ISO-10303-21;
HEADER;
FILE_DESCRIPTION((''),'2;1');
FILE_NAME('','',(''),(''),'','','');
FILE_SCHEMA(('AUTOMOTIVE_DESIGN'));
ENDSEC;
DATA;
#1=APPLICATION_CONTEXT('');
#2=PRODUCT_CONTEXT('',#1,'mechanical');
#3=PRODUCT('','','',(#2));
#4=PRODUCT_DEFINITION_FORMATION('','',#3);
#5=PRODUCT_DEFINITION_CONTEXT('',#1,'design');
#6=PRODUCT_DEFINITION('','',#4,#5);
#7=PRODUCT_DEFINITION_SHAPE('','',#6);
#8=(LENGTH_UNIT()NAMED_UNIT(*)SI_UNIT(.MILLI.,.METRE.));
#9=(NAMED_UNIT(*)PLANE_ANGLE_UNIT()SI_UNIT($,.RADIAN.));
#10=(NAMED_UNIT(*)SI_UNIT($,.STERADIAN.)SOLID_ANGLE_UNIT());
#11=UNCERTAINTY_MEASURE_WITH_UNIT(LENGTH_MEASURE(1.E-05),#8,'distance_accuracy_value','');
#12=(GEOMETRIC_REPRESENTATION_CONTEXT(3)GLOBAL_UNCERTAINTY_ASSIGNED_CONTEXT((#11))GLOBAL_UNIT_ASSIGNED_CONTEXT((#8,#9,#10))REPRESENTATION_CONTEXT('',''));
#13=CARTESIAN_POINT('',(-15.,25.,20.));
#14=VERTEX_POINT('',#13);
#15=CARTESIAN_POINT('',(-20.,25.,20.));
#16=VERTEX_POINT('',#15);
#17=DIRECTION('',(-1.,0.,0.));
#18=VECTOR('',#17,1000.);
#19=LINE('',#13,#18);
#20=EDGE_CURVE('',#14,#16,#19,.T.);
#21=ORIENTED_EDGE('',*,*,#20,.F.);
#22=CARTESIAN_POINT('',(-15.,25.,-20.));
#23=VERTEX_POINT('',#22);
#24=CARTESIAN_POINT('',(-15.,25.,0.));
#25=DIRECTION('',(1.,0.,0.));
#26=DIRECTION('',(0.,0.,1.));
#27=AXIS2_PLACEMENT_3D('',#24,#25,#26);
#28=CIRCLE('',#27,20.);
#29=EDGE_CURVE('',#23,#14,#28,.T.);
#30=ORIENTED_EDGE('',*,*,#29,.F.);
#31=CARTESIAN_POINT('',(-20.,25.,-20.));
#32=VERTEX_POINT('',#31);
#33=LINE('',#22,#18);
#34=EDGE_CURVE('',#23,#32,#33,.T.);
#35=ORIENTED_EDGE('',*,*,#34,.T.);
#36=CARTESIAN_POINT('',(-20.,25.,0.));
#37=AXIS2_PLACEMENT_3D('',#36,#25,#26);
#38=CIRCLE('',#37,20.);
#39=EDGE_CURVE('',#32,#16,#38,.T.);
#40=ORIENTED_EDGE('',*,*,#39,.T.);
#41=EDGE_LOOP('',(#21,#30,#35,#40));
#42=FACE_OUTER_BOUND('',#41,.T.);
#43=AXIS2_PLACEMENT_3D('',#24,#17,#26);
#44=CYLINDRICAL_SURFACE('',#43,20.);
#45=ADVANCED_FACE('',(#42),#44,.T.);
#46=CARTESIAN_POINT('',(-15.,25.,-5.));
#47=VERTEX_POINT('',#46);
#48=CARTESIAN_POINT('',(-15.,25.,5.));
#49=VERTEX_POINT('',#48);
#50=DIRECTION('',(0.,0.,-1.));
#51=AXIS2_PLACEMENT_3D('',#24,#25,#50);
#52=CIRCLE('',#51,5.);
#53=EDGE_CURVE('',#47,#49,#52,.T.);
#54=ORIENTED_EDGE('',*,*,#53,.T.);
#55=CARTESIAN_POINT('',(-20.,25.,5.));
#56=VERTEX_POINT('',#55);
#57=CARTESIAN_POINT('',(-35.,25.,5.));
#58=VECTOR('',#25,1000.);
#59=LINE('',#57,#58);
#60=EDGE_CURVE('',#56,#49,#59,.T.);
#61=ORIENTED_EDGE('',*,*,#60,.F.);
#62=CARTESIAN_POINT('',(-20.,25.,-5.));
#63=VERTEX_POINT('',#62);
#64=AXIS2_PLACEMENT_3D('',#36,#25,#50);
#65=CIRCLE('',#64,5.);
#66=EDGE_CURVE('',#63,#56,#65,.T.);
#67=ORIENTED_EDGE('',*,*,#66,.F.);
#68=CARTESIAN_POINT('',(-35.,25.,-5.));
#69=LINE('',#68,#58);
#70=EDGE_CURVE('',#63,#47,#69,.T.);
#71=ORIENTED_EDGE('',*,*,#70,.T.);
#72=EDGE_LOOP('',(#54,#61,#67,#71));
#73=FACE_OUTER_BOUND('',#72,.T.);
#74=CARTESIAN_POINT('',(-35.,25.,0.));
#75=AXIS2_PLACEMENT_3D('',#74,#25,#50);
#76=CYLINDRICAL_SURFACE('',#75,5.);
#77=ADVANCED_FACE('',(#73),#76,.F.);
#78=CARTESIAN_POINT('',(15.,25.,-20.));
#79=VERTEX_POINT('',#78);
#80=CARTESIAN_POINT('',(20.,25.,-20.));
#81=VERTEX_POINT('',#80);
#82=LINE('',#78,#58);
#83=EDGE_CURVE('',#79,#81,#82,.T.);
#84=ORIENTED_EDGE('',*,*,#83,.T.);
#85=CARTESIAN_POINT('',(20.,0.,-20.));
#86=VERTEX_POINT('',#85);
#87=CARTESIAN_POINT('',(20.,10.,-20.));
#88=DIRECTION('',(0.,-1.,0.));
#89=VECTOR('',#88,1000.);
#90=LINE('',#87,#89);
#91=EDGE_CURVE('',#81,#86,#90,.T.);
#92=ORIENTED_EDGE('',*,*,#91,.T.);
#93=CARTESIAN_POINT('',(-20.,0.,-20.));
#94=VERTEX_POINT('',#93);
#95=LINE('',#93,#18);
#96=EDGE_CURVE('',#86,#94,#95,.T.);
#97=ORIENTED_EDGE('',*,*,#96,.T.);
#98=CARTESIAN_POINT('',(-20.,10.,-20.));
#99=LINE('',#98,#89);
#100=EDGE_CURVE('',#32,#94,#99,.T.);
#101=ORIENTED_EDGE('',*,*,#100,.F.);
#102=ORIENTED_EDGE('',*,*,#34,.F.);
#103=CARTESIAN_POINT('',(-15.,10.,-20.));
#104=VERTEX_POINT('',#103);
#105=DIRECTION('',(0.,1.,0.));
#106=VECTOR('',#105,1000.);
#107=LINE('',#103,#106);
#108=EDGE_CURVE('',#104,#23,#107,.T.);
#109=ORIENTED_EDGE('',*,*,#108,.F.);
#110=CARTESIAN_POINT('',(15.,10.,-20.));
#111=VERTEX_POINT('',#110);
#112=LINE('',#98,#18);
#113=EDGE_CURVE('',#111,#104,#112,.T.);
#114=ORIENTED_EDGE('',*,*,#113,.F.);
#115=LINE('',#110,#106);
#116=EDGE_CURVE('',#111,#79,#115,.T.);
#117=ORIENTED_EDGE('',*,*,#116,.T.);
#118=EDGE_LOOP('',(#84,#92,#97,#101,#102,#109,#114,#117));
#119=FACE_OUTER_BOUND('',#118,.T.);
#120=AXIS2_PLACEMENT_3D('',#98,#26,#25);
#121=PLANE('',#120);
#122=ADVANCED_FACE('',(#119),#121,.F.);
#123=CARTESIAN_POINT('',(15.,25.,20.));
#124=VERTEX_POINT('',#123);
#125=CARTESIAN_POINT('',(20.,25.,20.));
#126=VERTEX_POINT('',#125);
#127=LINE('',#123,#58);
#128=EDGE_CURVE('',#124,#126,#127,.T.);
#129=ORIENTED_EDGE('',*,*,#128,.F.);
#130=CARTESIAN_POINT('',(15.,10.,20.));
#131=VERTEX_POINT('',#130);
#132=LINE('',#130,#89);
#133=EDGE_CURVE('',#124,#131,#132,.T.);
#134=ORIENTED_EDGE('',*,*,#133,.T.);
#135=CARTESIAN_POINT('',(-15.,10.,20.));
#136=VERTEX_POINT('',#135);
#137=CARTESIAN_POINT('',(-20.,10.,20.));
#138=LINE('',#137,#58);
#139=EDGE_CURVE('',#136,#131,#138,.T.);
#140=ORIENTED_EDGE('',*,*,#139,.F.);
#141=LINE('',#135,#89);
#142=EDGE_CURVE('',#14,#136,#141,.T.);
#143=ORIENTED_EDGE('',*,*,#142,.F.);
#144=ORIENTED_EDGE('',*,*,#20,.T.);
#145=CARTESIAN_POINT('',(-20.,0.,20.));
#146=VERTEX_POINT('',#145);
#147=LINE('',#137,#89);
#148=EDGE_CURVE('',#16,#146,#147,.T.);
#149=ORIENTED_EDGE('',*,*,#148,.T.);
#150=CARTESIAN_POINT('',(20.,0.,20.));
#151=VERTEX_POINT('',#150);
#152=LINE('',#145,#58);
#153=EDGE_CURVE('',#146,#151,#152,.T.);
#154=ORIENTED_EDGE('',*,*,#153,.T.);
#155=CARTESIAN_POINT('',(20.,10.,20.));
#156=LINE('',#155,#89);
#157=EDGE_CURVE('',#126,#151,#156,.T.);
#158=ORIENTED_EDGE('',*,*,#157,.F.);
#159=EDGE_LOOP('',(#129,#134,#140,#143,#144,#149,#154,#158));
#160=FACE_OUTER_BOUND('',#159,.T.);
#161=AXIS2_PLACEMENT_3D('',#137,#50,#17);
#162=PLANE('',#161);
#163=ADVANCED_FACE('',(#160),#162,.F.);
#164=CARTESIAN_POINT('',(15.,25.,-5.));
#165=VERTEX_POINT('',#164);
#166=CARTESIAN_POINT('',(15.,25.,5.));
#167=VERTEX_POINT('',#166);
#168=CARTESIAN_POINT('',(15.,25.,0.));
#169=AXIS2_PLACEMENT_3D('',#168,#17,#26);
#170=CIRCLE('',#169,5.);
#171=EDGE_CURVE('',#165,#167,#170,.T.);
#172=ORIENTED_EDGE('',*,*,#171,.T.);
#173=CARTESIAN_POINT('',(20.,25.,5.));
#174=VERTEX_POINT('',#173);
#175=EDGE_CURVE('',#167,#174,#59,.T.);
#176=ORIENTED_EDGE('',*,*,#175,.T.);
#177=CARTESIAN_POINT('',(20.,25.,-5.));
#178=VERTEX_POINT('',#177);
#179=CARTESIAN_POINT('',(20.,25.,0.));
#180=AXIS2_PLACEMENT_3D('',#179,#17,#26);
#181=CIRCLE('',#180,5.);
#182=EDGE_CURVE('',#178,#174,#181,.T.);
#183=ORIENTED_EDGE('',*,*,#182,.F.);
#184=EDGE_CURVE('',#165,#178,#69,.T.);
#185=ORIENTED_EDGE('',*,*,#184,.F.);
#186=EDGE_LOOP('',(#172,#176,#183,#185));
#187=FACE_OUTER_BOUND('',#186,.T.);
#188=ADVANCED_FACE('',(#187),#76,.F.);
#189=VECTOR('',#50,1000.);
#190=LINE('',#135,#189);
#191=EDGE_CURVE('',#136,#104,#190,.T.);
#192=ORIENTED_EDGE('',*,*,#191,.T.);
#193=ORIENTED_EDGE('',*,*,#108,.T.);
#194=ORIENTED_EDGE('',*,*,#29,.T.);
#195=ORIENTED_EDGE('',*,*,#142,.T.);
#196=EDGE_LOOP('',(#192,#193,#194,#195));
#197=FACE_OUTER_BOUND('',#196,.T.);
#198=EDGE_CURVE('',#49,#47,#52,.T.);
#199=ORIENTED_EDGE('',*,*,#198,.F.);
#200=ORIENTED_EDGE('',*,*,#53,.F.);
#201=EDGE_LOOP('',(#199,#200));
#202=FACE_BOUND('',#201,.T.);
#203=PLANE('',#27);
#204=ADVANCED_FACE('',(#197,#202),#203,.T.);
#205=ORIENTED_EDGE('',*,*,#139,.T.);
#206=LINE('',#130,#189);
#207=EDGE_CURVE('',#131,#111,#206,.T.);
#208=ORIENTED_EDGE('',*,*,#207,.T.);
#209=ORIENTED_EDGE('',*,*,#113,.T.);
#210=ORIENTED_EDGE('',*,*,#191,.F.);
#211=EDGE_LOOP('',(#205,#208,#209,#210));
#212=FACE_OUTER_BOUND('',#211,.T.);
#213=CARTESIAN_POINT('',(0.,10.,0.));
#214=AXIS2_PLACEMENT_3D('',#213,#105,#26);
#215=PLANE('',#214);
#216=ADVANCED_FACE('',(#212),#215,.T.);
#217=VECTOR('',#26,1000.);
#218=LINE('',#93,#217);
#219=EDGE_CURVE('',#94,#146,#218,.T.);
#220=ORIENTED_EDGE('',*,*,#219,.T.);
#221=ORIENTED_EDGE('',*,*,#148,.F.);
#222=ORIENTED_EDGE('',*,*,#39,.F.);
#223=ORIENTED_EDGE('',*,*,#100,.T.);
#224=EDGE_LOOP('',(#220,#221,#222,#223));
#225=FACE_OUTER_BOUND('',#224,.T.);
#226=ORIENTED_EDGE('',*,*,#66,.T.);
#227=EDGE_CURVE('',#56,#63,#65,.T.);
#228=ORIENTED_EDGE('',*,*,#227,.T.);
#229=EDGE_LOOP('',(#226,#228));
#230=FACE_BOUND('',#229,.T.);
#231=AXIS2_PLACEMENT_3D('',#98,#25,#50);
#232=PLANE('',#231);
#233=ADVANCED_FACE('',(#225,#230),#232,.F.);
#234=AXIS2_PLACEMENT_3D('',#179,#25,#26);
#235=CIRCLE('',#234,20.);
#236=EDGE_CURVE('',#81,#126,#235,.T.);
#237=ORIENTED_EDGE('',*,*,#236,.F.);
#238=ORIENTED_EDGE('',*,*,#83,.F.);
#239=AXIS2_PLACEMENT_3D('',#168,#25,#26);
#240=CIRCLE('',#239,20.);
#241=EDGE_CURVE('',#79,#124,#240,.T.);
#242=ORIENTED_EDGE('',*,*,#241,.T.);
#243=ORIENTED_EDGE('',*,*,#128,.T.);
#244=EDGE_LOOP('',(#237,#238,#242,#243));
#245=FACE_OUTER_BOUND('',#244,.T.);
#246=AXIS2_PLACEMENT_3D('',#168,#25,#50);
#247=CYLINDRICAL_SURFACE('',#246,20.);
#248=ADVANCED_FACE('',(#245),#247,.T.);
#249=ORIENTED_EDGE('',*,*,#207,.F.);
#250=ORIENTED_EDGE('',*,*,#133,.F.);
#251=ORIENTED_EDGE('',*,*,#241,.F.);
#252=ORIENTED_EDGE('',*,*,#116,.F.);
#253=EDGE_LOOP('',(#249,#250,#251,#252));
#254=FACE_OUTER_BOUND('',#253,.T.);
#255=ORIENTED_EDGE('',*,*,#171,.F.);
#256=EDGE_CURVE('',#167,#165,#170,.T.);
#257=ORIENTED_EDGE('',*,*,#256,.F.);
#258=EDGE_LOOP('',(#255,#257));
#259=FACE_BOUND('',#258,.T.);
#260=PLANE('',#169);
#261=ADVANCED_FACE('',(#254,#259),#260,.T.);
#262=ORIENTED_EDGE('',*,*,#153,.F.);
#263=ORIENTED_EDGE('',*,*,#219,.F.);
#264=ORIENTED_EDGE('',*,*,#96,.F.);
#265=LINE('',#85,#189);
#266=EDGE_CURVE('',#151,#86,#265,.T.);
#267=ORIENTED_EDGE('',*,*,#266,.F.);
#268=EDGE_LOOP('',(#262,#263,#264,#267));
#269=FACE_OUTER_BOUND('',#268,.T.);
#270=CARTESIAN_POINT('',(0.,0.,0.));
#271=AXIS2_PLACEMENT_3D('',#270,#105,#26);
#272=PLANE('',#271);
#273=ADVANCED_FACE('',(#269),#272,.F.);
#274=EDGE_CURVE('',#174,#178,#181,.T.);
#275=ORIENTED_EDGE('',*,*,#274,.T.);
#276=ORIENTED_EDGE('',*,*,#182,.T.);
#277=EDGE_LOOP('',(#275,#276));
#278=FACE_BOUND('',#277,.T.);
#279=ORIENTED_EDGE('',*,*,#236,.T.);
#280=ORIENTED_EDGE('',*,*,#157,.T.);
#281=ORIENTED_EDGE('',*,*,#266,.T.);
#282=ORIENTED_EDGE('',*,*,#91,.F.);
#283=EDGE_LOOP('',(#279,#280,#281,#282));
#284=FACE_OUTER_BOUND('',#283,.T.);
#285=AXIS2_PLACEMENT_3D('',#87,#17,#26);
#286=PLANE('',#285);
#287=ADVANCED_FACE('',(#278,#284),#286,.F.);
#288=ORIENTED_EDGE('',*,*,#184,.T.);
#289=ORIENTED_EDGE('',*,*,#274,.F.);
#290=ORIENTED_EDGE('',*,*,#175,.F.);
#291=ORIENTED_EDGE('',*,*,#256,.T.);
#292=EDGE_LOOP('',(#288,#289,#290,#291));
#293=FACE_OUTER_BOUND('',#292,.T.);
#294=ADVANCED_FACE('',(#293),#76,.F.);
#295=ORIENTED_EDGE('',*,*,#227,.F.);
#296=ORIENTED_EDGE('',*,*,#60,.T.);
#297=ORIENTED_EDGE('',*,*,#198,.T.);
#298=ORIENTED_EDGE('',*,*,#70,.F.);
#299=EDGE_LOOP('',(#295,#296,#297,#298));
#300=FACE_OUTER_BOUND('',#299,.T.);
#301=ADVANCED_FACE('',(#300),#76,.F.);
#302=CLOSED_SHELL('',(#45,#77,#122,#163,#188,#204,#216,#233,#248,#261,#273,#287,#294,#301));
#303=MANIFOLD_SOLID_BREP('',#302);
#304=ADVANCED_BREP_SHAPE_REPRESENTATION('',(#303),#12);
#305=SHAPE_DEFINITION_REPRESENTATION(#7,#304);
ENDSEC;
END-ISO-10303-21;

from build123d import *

# Parameters (mm, degrees)
SKETCH1_W           = 40
SKETCH1_H           = 40
BOSS_EXTRUDE1_DEPTH = 10
BOSS_EXTRUDE2_DEPTH = 5
SKETCH4_R           = 5
CUT_EXTRUDE1_DEPTH  = 52.5


with BuildPart() as part:
    # Sketch1 → Boss-Extrude1 (new body)
    with BuildSketch(Plane(origin=(0, 0, 0), x_dir=(1, 0, 0), z_dir=(0, 1, 0))):
        Rectangle(SKETCH1_W, SKETCH1_H)
    extrude(amount=BOSS_EXTRUDE1_DEPTH)

    # Sketch2 → Boss-Extrude2 (add)
    with BuildSketch(Plane(origin=(20, 0, 0), x_dir=(0, 0, -1), z_dir=(1, 0, 0))):
        with BuildLine():
            Line((-20, 10), (-20, 25))
            ThreePointArc((-20, 25), (0, 45), (20, 25))
            Line((20, 25), (20, 10))
            Line((20, 10), (-20, 10))
        make_face()
    boss_extrude2 = extrude(amount=-BOSS_EXTRUDE2_DEPTH)

    # Mirror1: Boss-Extrude2 across plane
    add(boss_extrude2.mirror(Plane(origin=(0, 0, 0), x_dir=(0, 0, 1), z_dir=(1, 0, 0))))

    # Sketch4 → Cut-Extrude1 (cut, symmetric)
    with BuildSketch(Plane(origin=(17.5, 0, 0), x_dir=(0, 0, -1), z_dir=(1, 0, 0))):
        with Locations((0, 25)):
            Circle(SKETCH4_R)
    extrude(amount=CUT_EXTRUDE1_DEPTH, both=True, mode=Mode.SUBTRACT)


solid = part.part
